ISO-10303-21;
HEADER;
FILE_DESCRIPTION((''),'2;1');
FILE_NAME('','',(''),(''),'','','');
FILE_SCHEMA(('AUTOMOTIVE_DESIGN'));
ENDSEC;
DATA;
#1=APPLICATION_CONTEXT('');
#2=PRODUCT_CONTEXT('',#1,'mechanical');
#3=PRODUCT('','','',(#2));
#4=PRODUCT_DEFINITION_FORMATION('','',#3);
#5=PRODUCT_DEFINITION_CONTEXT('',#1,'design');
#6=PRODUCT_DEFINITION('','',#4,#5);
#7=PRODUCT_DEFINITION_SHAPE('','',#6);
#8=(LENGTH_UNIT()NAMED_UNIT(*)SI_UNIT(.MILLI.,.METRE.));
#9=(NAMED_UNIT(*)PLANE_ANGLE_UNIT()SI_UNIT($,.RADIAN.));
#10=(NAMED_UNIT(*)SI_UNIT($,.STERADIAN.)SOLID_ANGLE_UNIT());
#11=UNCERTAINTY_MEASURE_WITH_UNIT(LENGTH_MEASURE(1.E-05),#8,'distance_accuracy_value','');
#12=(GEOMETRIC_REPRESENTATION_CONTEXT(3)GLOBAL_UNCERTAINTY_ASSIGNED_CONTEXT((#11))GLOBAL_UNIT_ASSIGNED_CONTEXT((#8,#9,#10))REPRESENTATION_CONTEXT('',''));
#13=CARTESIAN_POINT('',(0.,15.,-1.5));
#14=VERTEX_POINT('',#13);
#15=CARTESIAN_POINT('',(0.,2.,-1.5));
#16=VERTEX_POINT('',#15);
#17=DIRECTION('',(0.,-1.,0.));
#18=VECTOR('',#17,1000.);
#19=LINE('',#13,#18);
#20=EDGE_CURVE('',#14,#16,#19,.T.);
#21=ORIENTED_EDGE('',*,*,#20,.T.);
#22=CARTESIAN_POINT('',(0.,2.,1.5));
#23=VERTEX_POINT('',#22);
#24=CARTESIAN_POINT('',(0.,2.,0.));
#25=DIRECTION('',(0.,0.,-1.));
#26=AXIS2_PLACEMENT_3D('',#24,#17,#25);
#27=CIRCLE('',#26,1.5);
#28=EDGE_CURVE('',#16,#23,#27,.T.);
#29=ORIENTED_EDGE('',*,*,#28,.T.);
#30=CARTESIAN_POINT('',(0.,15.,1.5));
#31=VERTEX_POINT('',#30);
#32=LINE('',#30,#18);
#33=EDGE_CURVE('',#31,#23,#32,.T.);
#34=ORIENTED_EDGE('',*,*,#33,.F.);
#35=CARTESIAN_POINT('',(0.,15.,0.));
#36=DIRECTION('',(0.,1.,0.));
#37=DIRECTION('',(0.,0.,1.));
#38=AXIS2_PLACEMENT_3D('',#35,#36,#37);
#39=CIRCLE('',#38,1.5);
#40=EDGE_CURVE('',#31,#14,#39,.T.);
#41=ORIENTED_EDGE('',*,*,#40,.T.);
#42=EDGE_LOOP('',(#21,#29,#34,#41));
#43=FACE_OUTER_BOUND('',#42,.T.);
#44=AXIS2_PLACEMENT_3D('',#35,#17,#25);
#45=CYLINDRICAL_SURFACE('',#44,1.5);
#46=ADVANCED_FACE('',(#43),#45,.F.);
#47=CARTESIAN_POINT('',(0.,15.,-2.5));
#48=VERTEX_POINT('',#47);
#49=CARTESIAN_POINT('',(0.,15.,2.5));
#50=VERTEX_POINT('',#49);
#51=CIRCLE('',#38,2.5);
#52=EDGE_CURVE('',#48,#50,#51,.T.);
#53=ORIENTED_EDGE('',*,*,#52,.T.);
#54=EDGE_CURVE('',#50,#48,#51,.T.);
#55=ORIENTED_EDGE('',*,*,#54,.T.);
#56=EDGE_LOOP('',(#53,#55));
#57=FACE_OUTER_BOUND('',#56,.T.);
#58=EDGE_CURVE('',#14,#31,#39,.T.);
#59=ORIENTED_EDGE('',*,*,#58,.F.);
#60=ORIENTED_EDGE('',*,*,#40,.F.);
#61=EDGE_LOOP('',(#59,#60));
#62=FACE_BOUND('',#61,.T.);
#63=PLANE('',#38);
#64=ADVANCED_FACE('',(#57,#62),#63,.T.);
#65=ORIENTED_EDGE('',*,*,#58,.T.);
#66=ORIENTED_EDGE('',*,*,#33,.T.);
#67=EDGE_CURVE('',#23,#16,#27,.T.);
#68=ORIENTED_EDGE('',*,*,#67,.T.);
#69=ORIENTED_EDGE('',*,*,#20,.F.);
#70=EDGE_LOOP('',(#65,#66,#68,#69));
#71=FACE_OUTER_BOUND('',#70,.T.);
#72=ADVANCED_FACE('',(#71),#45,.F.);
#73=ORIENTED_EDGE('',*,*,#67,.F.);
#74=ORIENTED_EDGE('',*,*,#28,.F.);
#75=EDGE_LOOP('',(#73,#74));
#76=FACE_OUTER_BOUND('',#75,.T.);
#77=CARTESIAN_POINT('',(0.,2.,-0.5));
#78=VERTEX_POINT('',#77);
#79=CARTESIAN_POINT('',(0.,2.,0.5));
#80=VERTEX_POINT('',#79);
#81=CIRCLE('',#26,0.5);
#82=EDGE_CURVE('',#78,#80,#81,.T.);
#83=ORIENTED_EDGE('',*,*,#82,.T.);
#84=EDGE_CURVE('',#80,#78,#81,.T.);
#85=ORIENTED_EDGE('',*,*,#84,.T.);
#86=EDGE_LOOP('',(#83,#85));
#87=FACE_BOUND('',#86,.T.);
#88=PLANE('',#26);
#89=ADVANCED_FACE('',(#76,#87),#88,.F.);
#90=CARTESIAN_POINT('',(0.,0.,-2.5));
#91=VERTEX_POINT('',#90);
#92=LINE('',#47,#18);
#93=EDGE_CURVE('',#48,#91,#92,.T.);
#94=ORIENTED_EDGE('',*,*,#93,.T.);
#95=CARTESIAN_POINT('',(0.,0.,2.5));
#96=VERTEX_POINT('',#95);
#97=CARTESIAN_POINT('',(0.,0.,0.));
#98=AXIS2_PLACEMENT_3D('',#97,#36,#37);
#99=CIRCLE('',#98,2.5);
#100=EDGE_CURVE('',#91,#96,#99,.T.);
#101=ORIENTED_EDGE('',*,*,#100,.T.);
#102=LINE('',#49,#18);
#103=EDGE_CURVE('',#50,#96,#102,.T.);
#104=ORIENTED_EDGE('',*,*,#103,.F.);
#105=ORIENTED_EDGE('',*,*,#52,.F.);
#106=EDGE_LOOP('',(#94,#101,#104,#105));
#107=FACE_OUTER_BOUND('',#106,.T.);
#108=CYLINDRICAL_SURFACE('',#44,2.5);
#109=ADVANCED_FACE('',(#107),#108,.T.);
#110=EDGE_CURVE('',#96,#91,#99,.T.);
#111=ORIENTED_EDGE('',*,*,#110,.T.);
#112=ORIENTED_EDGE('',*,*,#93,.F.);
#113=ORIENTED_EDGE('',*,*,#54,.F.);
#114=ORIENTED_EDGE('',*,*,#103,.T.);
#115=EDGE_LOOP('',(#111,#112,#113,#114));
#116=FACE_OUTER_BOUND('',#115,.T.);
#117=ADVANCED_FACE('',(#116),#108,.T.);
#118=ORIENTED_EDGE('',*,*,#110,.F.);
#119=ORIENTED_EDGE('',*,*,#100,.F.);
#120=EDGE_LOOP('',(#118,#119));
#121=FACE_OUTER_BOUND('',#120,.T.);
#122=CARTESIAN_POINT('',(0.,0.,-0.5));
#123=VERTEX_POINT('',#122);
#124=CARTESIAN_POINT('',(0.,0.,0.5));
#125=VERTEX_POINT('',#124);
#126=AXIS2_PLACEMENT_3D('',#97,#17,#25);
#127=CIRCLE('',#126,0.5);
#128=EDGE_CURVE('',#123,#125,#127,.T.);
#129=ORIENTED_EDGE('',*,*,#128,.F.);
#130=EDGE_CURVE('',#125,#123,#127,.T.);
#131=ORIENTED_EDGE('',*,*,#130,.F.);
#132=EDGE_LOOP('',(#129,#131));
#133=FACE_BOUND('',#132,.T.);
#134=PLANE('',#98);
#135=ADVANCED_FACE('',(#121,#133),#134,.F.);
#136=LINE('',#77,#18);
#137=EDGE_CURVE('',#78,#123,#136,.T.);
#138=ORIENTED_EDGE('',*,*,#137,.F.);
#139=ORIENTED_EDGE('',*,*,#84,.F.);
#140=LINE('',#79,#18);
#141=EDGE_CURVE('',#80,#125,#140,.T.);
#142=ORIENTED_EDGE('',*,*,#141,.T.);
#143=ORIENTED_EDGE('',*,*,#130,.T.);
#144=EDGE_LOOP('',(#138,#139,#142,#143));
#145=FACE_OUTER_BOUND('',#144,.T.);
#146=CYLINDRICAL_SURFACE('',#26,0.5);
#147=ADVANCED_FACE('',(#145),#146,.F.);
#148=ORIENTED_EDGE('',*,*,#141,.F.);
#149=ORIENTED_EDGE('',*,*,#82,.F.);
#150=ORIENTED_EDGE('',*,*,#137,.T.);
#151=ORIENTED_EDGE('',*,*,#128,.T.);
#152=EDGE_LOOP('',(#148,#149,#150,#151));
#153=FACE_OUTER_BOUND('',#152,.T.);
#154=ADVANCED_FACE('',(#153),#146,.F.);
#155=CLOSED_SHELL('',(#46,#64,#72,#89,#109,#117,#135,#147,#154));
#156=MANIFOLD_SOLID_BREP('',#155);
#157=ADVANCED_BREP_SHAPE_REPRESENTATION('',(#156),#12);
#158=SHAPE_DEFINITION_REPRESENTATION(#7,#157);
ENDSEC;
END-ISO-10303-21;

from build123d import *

# Parameters (mm, degrees)
SKETCH1_R           = 2.5
SKETCH1_R_2         = 1.5
BOSS_EXTRUDE1_DEPTH = 15
SKETCH2_R           = 1.5
SKETCH2_R_2         = 0.5
BOSS_EXTRUDE2_DEPTH = 2


with BuildPart() as part:
    # Sketch1 → Boss-Extrude1 (new body)
    with BuildSketch(Plane(origin=(0, 0, 0), x_dir=(1, 0, 0), z_dir=(0, 1, 0))):
        with Locations(Location((0, 0, 0), (0, 0, 270))):
            Circle(SKETCH1_R)
        with Locations(Location((0, 0, 0), (0, 0, 270))):
            Circle(SKETCH1_R_2, mode=Mode.SUBTRACT)
    extrude(amount=BOSS_EXTRUDE1_DEPTH)

    # Sketch2 → Boss-Extrude2 (add)
    with BuildSketch(Plane.XZ):
        with Locations(Location((0, 0, 0), (0, 0, 270))):
            Circle(SKETCH2_R)
        with Locations(Location((0, 0, 0), (0, 0, 270))):
            Circle(SKETCH2_R_2, mode=Mode.SUBTRACT)
    extrude(amount=-BOSS_EXTRUDE2_DEPTH)


solid = part.part
